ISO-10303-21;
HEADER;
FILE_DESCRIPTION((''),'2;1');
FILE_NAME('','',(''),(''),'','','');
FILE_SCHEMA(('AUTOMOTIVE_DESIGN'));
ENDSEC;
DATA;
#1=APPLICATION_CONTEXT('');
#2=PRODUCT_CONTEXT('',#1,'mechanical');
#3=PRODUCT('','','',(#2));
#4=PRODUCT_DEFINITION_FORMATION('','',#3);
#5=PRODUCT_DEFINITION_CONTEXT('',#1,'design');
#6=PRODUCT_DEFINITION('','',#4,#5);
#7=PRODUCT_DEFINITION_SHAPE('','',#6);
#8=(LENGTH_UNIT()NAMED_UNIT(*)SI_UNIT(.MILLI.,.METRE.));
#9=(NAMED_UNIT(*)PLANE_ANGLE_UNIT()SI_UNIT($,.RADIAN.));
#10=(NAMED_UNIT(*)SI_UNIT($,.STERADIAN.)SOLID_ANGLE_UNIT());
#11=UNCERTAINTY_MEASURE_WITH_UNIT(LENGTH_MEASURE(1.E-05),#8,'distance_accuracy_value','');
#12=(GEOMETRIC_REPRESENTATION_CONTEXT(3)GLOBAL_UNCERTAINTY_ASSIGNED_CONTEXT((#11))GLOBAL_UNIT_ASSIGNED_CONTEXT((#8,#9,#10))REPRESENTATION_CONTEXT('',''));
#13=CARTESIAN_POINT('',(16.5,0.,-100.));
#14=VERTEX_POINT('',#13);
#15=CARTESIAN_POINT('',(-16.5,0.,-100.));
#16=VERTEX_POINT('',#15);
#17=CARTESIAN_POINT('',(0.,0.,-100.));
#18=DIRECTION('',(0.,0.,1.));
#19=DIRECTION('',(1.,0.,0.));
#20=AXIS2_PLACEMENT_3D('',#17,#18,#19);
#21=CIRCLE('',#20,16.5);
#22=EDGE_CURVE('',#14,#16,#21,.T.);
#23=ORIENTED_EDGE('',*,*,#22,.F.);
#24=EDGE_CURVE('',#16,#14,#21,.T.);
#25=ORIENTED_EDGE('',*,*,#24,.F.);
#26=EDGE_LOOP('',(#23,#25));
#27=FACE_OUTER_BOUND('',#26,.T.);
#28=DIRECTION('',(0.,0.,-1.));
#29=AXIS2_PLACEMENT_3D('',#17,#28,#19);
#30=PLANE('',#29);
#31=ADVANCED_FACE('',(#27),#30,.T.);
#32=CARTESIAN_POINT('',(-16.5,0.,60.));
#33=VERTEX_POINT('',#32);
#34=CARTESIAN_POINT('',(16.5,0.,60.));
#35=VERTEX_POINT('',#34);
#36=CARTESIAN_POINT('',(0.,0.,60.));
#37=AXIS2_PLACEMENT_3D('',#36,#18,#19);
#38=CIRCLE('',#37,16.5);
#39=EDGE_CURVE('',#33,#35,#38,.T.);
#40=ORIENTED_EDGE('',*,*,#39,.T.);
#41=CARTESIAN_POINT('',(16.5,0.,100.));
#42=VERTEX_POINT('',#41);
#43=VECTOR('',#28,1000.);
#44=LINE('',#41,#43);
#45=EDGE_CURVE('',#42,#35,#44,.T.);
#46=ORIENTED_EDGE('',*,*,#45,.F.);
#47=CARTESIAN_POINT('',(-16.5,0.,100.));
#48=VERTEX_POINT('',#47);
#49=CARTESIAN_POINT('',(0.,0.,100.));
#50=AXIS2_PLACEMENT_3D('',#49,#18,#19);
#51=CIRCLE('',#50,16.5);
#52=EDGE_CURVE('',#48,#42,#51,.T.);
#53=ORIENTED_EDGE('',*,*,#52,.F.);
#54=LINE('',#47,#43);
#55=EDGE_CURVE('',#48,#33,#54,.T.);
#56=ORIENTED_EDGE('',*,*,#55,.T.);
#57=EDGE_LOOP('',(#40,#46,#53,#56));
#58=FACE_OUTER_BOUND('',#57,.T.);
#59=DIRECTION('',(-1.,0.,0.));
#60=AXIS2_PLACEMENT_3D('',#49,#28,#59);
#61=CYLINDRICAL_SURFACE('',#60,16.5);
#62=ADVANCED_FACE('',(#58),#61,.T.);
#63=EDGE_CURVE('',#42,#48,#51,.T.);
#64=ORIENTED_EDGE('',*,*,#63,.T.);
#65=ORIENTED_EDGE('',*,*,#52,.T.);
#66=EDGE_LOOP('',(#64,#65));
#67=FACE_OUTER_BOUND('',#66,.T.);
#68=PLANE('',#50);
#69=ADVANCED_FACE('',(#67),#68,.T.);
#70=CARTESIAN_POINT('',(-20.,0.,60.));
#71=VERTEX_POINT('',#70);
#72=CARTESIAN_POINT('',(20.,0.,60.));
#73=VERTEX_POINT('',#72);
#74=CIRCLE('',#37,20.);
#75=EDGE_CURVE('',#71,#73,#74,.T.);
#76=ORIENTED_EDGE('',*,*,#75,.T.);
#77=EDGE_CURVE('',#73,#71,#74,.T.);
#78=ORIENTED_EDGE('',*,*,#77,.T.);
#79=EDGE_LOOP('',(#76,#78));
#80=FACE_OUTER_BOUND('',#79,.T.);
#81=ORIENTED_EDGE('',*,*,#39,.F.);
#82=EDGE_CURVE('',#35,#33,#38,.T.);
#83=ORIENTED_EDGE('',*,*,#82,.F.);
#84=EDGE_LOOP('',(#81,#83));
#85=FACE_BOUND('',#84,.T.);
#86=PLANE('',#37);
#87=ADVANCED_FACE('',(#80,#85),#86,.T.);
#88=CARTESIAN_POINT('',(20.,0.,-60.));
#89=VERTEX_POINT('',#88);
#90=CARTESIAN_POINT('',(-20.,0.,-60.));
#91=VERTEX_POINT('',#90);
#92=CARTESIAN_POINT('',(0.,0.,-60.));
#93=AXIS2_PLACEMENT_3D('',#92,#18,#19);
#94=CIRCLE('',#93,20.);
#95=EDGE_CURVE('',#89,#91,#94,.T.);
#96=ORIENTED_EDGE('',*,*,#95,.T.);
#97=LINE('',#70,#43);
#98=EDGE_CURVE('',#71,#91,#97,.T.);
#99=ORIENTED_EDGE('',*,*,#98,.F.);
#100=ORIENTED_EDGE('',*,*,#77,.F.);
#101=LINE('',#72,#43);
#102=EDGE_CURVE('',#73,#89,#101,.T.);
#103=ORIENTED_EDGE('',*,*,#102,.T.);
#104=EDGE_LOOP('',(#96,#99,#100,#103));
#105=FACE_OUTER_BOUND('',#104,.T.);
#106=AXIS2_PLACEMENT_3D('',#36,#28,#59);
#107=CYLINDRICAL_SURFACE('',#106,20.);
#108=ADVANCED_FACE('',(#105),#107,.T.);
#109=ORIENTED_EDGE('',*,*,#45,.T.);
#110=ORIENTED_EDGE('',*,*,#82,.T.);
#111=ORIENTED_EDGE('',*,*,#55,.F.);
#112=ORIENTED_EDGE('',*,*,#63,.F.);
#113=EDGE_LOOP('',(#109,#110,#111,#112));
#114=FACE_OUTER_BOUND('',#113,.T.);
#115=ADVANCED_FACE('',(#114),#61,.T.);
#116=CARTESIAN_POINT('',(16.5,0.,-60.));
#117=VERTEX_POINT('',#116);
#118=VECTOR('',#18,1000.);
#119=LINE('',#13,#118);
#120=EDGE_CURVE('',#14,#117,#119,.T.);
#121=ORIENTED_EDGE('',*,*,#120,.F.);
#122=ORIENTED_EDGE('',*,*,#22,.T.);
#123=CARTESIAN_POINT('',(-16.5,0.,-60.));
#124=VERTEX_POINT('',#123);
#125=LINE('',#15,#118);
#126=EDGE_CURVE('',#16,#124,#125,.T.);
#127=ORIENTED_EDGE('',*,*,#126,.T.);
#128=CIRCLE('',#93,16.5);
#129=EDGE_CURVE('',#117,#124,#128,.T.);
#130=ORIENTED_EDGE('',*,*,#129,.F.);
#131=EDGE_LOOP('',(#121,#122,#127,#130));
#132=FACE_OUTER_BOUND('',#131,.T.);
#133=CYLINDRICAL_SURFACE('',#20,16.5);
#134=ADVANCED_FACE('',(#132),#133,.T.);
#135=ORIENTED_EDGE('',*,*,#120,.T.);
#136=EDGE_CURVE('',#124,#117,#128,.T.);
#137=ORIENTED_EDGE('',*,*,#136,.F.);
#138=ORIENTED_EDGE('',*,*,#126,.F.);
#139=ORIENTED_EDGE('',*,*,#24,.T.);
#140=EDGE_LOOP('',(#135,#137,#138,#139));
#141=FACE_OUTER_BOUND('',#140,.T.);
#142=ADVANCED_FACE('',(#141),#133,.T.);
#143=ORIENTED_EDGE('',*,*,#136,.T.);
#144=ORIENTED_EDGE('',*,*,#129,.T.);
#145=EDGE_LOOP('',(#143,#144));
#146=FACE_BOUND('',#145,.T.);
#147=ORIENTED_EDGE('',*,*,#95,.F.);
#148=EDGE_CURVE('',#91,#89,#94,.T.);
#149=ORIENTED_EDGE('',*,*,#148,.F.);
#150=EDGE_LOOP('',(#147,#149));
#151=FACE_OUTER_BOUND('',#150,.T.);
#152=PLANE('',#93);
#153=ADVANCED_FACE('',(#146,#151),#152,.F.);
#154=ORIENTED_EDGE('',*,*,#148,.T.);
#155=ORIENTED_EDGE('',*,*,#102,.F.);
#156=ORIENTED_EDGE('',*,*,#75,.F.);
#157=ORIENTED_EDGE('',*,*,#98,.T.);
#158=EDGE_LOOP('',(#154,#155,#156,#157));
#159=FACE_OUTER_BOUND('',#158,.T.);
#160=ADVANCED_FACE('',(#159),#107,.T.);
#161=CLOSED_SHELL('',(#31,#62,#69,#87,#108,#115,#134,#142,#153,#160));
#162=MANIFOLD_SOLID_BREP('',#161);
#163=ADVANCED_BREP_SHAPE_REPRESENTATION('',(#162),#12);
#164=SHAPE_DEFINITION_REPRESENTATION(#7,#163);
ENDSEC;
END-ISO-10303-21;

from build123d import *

# Parameters (mm, degrees)
SKETCH_1_R           = 20
BOSS_EXTRUDE_1_DEPTH = 60
SKETCH_2_R           = 16.5
BOSS_EXTRUDE_2_DEPTH = 40


with BuildPart() as part:
    # Sketch 1 → Boss-Extrude 1 (new, symmetric)
    with BuildSketch(Plane.XY):
        Circle(SKETCH_1_R)
    extrude(amount=BOSS_EXTRUDE_1_DEPTH, both=True)

    # Sketch 2 → Boss-Extrude 2 (add)
    with BuildSketch(Plane.XY.offset(60)):
        Circle(SKETCH_2_R)
    boss_extrude_2 = extrude(amount=BOSS_EXTRUDE_2_DEPTH)

    # Mirror 1: Boss-Extrude 2 across plane
    add(boss_extrude_2.mirror(Plane.XY))


solid = part.part
